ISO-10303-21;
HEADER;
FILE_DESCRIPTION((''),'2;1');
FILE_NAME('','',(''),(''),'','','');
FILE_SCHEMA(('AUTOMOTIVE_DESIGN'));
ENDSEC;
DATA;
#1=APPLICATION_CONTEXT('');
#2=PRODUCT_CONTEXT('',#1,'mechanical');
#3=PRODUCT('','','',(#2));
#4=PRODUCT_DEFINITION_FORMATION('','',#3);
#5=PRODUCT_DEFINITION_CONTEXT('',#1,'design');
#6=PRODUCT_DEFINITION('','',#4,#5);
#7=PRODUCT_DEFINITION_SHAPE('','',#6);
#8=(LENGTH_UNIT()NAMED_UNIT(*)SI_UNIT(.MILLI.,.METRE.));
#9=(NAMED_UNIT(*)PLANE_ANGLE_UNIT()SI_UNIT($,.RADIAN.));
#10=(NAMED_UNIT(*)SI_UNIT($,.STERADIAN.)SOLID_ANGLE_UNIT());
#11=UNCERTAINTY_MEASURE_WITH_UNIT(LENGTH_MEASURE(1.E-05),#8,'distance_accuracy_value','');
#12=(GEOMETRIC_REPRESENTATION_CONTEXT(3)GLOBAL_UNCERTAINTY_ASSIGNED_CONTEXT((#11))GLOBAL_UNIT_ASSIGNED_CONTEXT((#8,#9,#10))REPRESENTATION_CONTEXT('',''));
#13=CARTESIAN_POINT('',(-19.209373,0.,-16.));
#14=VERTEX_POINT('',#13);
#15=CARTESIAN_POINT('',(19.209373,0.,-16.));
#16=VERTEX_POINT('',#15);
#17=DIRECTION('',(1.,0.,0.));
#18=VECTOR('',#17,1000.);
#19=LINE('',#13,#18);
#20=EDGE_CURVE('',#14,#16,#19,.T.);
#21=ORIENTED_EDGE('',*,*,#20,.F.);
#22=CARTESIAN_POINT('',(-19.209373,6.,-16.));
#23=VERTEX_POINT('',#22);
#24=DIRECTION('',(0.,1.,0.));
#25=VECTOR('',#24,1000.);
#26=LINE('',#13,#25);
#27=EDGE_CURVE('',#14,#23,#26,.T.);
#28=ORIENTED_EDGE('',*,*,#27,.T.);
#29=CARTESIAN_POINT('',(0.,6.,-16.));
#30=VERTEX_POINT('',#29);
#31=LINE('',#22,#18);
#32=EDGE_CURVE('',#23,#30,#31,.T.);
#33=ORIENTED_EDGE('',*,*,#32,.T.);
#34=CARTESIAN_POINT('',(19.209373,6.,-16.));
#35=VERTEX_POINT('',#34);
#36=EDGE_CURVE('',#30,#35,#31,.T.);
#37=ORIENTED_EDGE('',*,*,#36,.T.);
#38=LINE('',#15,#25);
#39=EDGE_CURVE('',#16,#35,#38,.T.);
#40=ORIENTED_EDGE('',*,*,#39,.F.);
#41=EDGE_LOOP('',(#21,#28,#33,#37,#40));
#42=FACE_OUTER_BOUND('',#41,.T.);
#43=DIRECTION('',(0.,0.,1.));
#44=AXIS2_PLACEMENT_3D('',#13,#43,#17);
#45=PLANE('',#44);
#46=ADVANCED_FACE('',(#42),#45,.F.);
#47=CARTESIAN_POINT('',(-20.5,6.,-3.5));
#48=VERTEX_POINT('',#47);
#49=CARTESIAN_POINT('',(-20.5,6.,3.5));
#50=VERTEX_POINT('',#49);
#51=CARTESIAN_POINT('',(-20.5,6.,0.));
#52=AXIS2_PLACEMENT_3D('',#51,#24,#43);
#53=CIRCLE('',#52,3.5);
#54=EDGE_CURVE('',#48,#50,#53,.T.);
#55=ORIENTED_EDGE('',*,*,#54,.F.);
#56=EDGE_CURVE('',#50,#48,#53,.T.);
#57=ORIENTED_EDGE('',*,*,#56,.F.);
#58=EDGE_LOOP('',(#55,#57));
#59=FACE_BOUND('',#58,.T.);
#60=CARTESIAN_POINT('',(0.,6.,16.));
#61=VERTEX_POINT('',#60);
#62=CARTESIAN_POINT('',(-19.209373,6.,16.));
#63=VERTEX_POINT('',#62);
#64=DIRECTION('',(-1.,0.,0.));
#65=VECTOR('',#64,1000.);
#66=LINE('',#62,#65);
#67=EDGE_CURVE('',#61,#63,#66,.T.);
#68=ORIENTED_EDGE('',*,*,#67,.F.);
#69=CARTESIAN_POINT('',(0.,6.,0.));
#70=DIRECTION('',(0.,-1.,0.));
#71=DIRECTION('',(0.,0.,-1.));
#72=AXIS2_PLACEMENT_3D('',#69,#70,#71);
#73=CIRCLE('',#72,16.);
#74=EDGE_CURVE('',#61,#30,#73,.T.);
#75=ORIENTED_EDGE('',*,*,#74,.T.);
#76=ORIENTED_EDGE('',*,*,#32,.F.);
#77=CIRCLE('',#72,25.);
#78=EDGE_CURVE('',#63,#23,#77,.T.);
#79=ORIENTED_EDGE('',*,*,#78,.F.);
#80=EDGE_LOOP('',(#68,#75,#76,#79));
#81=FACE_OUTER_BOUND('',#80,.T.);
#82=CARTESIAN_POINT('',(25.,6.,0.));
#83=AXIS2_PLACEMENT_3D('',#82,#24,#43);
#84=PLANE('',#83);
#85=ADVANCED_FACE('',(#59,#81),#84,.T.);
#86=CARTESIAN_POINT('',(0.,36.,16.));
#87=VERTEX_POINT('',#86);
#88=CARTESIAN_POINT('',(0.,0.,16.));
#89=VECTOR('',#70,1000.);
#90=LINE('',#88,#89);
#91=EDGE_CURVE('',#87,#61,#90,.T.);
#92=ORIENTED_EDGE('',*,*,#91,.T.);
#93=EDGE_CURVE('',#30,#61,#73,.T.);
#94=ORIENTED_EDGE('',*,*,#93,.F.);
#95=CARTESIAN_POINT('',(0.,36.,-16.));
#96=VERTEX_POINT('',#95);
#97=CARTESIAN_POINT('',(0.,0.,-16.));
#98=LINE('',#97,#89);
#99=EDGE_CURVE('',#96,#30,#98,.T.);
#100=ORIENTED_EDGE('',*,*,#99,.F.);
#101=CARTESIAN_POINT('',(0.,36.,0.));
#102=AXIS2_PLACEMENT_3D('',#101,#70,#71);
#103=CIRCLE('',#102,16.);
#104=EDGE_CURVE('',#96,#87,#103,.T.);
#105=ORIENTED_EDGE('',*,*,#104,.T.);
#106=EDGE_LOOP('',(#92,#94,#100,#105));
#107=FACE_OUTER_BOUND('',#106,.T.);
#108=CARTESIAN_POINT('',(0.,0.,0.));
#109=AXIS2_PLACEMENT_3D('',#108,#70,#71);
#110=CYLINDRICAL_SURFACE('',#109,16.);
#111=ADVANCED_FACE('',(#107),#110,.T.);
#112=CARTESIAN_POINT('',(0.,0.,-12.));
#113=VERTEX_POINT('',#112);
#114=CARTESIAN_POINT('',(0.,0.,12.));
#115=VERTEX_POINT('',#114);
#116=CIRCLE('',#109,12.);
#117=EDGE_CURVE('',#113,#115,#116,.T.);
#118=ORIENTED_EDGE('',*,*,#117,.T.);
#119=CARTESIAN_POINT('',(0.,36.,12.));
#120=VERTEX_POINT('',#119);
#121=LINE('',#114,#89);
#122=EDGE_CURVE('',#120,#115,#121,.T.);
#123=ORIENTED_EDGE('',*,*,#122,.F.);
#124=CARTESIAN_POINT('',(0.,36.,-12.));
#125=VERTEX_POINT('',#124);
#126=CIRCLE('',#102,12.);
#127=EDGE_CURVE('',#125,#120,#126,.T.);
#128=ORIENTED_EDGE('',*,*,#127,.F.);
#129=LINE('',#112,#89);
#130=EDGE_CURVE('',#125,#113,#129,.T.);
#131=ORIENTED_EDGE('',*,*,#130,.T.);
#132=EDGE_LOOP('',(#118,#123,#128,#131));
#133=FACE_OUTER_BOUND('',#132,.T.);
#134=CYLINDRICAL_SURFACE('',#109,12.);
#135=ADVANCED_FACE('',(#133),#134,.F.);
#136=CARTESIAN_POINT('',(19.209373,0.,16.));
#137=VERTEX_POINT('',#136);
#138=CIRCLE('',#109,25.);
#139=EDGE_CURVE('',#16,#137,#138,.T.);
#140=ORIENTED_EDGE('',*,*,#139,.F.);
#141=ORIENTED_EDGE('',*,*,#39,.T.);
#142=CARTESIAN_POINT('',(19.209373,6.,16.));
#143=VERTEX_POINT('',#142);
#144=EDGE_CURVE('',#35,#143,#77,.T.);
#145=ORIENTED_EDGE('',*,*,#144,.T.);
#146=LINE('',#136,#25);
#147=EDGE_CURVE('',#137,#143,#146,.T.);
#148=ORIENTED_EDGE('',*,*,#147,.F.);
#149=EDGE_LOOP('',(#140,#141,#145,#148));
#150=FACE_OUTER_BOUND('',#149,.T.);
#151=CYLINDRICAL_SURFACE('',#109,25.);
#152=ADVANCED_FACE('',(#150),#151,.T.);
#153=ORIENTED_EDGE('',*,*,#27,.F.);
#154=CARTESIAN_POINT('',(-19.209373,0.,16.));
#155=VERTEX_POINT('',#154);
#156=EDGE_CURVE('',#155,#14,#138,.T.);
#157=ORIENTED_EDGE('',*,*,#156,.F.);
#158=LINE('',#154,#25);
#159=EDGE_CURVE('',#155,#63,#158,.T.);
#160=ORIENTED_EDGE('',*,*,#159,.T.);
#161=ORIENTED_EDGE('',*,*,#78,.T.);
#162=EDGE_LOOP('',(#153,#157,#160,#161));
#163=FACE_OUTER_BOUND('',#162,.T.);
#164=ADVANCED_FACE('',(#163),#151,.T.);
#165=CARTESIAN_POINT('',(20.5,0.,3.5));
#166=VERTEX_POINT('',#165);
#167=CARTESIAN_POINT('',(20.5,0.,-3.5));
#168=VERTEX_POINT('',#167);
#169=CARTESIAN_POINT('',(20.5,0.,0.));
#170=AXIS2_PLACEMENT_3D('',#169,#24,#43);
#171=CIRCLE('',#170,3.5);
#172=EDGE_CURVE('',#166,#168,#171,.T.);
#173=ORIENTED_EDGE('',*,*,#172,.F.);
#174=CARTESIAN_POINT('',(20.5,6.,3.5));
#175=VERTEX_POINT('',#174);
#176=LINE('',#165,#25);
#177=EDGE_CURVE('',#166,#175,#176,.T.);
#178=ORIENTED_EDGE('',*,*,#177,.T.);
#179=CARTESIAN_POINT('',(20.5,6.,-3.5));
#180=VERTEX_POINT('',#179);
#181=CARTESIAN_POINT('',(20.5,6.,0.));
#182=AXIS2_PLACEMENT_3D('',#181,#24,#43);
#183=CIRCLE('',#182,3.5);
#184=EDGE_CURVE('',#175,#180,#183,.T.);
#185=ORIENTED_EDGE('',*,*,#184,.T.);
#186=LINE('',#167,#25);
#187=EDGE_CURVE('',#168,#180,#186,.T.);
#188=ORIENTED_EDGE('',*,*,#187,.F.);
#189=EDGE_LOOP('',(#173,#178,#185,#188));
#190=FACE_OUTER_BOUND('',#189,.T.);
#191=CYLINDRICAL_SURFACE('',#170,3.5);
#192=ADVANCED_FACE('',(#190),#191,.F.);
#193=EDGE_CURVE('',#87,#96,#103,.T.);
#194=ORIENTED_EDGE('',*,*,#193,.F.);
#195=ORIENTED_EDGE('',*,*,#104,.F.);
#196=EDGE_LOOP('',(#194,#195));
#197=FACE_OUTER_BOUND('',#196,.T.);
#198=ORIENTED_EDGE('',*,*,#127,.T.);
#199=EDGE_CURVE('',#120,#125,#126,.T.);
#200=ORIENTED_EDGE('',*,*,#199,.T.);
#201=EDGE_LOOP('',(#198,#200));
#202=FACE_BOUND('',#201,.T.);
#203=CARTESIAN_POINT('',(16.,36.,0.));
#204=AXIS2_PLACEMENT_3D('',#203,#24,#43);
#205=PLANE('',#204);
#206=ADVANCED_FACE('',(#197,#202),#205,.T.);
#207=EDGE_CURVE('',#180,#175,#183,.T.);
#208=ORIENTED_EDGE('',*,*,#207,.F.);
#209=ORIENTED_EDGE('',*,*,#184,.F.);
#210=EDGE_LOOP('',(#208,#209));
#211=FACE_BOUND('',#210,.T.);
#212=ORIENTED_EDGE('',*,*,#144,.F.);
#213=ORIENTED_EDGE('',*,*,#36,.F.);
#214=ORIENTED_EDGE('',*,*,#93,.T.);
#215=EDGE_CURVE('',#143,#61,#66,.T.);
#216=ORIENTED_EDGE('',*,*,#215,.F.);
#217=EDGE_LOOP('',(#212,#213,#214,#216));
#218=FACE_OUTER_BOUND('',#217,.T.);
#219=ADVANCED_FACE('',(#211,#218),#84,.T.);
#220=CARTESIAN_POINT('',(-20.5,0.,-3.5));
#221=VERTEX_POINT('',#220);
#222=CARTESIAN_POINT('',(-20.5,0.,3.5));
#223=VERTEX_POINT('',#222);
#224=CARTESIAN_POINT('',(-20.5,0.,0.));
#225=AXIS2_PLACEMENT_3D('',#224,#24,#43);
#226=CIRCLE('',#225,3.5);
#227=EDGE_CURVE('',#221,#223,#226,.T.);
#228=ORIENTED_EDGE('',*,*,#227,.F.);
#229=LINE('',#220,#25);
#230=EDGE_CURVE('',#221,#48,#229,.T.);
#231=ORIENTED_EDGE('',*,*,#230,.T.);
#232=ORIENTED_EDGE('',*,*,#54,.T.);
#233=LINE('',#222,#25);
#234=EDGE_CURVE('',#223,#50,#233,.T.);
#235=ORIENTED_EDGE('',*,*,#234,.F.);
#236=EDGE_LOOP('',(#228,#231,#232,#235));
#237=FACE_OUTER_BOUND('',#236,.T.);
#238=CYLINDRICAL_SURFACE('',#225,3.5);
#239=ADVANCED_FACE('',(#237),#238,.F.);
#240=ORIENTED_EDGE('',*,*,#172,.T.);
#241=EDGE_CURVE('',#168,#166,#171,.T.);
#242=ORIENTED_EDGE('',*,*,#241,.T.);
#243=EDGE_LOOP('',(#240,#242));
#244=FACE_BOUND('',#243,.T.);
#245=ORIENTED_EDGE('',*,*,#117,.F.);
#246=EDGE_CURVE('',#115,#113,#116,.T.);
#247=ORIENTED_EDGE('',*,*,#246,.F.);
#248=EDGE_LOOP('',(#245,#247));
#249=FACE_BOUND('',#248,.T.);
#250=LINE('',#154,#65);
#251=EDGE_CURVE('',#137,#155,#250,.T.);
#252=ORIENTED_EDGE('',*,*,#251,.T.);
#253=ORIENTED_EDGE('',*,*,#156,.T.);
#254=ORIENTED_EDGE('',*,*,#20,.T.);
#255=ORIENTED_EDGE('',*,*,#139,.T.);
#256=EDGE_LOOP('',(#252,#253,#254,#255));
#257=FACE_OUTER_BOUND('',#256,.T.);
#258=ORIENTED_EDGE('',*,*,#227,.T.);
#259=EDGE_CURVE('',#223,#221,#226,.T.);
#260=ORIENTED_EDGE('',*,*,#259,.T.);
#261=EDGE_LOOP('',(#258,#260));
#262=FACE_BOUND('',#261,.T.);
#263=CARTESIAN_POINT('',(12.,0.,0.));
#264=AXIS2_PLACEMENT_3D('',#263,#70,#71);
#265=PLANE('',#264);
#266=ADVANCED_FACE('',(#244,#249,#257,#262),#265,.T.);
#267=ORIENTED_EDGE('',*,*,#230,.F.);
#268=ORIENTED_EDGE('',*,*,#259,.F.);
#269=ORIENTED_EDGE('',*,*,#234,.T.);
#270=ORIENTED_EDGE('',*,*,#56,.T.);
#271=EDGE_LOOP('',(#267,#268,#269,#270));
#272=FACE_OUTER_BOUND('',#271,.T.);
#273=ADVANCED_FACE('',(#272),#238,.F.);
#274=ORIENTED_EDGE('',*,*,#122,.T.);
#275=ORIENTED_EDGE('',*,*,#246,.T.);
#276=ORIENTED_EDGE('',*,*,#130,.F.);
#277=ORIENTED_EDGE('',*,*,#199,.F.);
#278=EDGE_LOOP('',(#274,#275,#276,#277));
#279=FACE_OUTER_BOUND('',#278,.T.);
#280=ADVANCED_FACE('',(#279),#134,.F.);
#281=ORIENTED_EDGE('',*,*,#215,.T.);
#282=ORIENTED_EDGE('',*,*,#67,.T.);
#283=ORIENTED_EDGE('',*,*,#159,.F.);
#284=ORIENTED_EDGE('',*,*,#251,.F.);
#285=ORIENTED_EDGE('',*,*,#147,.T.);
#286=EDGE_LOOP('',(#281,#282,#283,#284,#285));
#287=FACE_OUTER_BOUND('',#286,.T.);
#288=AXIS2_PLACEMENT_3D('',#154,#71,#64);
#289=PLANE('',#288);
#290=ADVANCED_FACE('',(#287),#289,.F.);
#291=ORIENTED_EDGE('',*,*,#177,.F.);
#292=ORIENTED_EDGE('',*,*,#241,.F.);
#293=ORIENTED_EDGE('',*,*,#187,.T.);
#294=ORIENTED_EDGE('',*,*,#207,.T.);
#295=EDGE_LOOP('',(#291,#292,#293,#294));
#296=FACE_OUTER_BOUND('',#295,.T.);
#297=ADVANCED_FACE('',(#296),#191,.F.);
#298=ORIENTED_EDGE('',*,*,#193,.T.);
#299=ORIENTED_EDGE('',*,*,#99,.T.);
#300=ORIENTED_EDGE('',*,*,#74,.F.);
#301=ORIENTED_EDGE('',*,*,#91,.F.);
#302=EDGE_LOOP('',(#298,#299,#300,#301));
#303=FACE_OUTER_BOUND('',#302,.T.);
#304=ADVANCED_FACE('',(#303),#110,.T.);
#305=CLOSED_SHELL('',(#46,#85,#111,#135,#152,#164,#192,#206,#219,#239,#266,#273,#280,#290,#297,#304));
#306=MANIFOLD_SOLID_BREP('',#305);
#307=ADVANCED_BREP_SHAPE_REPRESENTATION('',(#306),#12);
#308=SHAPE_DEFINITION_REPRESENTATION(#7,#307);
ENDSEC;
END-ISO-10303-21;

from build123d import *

# Parameters (mm, degrees)
SKETCH2_R          = 3.5
CUT_EXTRUDE1_DEPTH = 47.368092477
CUT_EXTRUDE2_DEPTH = 47.368092477


with BuildPart() as part:
    # Sketch1 → Revolve1 (revolve)
    with BuildSketch(Plane.XY, mode=Mode.PRIVATE) as revolve1_sk:
        Polygon((12, 36), (12, 0), (25, 0), (25, 6), (16, 6), (16, 36), align=None)
    revolve(revolve1_sk.sketch.rotate(Axis((0, 0, 0), (0, 1, 0)), 90), axis=Axis((0, 0, 0), (0, 1, 0)))

    # Sketch2 → Cut-Extrude1 (cut, through all)
    with BuildSketch(Plane(origin=(0, 6, 0), x_dir=(1, 0, 0), z_dir=(0, 1, 0))):
        with Locations(Location((-20.5, 0, 0), (0, 0, 270))):
            Circle(SKETCH2_R)
        with Locations(Location((0, 20.5, 0), (0, 0, 270))):
            Circle(SKETCH2_R)
        with Locations(Location((20.5, 0, 0), (0, 0, 270))):
            Circle(SKETCH2_R)
        with Locations(Location((0, -20.5, 0), (0, 0, 270))):
            Circle(SKETCH2_R)
    extrude(amount=-CUT_EXTRUDE1_DEPTH, mode=Mode.SUBTRACT)

    # Sketch3 → Cut-Extrude2 (cut, through all)
    with BuildSketch(Plane(origin=(0, 6, 0), x_dir=(1, 0, 0), z_dir=(0, 1, 0))):
        with BuildLine():
            Line((-19.209372712, 16), (19.209372712, 16))
            ThreePointArc((19.209372712, 16), (0, 25), (-19.209372712, 16))
        make_face()
        with BuildLine():
            Line((-19.209372712, -16), (19.209372712, -16))
            ThreePointArc((19.209372712, -16), (0, -25), (-19.209372712, -16))
        make_face()
    extrude(amount=-CUT_EXTRUDE2_DEPTH, mode=Mode.SUBTRACT)


solid = part.part
